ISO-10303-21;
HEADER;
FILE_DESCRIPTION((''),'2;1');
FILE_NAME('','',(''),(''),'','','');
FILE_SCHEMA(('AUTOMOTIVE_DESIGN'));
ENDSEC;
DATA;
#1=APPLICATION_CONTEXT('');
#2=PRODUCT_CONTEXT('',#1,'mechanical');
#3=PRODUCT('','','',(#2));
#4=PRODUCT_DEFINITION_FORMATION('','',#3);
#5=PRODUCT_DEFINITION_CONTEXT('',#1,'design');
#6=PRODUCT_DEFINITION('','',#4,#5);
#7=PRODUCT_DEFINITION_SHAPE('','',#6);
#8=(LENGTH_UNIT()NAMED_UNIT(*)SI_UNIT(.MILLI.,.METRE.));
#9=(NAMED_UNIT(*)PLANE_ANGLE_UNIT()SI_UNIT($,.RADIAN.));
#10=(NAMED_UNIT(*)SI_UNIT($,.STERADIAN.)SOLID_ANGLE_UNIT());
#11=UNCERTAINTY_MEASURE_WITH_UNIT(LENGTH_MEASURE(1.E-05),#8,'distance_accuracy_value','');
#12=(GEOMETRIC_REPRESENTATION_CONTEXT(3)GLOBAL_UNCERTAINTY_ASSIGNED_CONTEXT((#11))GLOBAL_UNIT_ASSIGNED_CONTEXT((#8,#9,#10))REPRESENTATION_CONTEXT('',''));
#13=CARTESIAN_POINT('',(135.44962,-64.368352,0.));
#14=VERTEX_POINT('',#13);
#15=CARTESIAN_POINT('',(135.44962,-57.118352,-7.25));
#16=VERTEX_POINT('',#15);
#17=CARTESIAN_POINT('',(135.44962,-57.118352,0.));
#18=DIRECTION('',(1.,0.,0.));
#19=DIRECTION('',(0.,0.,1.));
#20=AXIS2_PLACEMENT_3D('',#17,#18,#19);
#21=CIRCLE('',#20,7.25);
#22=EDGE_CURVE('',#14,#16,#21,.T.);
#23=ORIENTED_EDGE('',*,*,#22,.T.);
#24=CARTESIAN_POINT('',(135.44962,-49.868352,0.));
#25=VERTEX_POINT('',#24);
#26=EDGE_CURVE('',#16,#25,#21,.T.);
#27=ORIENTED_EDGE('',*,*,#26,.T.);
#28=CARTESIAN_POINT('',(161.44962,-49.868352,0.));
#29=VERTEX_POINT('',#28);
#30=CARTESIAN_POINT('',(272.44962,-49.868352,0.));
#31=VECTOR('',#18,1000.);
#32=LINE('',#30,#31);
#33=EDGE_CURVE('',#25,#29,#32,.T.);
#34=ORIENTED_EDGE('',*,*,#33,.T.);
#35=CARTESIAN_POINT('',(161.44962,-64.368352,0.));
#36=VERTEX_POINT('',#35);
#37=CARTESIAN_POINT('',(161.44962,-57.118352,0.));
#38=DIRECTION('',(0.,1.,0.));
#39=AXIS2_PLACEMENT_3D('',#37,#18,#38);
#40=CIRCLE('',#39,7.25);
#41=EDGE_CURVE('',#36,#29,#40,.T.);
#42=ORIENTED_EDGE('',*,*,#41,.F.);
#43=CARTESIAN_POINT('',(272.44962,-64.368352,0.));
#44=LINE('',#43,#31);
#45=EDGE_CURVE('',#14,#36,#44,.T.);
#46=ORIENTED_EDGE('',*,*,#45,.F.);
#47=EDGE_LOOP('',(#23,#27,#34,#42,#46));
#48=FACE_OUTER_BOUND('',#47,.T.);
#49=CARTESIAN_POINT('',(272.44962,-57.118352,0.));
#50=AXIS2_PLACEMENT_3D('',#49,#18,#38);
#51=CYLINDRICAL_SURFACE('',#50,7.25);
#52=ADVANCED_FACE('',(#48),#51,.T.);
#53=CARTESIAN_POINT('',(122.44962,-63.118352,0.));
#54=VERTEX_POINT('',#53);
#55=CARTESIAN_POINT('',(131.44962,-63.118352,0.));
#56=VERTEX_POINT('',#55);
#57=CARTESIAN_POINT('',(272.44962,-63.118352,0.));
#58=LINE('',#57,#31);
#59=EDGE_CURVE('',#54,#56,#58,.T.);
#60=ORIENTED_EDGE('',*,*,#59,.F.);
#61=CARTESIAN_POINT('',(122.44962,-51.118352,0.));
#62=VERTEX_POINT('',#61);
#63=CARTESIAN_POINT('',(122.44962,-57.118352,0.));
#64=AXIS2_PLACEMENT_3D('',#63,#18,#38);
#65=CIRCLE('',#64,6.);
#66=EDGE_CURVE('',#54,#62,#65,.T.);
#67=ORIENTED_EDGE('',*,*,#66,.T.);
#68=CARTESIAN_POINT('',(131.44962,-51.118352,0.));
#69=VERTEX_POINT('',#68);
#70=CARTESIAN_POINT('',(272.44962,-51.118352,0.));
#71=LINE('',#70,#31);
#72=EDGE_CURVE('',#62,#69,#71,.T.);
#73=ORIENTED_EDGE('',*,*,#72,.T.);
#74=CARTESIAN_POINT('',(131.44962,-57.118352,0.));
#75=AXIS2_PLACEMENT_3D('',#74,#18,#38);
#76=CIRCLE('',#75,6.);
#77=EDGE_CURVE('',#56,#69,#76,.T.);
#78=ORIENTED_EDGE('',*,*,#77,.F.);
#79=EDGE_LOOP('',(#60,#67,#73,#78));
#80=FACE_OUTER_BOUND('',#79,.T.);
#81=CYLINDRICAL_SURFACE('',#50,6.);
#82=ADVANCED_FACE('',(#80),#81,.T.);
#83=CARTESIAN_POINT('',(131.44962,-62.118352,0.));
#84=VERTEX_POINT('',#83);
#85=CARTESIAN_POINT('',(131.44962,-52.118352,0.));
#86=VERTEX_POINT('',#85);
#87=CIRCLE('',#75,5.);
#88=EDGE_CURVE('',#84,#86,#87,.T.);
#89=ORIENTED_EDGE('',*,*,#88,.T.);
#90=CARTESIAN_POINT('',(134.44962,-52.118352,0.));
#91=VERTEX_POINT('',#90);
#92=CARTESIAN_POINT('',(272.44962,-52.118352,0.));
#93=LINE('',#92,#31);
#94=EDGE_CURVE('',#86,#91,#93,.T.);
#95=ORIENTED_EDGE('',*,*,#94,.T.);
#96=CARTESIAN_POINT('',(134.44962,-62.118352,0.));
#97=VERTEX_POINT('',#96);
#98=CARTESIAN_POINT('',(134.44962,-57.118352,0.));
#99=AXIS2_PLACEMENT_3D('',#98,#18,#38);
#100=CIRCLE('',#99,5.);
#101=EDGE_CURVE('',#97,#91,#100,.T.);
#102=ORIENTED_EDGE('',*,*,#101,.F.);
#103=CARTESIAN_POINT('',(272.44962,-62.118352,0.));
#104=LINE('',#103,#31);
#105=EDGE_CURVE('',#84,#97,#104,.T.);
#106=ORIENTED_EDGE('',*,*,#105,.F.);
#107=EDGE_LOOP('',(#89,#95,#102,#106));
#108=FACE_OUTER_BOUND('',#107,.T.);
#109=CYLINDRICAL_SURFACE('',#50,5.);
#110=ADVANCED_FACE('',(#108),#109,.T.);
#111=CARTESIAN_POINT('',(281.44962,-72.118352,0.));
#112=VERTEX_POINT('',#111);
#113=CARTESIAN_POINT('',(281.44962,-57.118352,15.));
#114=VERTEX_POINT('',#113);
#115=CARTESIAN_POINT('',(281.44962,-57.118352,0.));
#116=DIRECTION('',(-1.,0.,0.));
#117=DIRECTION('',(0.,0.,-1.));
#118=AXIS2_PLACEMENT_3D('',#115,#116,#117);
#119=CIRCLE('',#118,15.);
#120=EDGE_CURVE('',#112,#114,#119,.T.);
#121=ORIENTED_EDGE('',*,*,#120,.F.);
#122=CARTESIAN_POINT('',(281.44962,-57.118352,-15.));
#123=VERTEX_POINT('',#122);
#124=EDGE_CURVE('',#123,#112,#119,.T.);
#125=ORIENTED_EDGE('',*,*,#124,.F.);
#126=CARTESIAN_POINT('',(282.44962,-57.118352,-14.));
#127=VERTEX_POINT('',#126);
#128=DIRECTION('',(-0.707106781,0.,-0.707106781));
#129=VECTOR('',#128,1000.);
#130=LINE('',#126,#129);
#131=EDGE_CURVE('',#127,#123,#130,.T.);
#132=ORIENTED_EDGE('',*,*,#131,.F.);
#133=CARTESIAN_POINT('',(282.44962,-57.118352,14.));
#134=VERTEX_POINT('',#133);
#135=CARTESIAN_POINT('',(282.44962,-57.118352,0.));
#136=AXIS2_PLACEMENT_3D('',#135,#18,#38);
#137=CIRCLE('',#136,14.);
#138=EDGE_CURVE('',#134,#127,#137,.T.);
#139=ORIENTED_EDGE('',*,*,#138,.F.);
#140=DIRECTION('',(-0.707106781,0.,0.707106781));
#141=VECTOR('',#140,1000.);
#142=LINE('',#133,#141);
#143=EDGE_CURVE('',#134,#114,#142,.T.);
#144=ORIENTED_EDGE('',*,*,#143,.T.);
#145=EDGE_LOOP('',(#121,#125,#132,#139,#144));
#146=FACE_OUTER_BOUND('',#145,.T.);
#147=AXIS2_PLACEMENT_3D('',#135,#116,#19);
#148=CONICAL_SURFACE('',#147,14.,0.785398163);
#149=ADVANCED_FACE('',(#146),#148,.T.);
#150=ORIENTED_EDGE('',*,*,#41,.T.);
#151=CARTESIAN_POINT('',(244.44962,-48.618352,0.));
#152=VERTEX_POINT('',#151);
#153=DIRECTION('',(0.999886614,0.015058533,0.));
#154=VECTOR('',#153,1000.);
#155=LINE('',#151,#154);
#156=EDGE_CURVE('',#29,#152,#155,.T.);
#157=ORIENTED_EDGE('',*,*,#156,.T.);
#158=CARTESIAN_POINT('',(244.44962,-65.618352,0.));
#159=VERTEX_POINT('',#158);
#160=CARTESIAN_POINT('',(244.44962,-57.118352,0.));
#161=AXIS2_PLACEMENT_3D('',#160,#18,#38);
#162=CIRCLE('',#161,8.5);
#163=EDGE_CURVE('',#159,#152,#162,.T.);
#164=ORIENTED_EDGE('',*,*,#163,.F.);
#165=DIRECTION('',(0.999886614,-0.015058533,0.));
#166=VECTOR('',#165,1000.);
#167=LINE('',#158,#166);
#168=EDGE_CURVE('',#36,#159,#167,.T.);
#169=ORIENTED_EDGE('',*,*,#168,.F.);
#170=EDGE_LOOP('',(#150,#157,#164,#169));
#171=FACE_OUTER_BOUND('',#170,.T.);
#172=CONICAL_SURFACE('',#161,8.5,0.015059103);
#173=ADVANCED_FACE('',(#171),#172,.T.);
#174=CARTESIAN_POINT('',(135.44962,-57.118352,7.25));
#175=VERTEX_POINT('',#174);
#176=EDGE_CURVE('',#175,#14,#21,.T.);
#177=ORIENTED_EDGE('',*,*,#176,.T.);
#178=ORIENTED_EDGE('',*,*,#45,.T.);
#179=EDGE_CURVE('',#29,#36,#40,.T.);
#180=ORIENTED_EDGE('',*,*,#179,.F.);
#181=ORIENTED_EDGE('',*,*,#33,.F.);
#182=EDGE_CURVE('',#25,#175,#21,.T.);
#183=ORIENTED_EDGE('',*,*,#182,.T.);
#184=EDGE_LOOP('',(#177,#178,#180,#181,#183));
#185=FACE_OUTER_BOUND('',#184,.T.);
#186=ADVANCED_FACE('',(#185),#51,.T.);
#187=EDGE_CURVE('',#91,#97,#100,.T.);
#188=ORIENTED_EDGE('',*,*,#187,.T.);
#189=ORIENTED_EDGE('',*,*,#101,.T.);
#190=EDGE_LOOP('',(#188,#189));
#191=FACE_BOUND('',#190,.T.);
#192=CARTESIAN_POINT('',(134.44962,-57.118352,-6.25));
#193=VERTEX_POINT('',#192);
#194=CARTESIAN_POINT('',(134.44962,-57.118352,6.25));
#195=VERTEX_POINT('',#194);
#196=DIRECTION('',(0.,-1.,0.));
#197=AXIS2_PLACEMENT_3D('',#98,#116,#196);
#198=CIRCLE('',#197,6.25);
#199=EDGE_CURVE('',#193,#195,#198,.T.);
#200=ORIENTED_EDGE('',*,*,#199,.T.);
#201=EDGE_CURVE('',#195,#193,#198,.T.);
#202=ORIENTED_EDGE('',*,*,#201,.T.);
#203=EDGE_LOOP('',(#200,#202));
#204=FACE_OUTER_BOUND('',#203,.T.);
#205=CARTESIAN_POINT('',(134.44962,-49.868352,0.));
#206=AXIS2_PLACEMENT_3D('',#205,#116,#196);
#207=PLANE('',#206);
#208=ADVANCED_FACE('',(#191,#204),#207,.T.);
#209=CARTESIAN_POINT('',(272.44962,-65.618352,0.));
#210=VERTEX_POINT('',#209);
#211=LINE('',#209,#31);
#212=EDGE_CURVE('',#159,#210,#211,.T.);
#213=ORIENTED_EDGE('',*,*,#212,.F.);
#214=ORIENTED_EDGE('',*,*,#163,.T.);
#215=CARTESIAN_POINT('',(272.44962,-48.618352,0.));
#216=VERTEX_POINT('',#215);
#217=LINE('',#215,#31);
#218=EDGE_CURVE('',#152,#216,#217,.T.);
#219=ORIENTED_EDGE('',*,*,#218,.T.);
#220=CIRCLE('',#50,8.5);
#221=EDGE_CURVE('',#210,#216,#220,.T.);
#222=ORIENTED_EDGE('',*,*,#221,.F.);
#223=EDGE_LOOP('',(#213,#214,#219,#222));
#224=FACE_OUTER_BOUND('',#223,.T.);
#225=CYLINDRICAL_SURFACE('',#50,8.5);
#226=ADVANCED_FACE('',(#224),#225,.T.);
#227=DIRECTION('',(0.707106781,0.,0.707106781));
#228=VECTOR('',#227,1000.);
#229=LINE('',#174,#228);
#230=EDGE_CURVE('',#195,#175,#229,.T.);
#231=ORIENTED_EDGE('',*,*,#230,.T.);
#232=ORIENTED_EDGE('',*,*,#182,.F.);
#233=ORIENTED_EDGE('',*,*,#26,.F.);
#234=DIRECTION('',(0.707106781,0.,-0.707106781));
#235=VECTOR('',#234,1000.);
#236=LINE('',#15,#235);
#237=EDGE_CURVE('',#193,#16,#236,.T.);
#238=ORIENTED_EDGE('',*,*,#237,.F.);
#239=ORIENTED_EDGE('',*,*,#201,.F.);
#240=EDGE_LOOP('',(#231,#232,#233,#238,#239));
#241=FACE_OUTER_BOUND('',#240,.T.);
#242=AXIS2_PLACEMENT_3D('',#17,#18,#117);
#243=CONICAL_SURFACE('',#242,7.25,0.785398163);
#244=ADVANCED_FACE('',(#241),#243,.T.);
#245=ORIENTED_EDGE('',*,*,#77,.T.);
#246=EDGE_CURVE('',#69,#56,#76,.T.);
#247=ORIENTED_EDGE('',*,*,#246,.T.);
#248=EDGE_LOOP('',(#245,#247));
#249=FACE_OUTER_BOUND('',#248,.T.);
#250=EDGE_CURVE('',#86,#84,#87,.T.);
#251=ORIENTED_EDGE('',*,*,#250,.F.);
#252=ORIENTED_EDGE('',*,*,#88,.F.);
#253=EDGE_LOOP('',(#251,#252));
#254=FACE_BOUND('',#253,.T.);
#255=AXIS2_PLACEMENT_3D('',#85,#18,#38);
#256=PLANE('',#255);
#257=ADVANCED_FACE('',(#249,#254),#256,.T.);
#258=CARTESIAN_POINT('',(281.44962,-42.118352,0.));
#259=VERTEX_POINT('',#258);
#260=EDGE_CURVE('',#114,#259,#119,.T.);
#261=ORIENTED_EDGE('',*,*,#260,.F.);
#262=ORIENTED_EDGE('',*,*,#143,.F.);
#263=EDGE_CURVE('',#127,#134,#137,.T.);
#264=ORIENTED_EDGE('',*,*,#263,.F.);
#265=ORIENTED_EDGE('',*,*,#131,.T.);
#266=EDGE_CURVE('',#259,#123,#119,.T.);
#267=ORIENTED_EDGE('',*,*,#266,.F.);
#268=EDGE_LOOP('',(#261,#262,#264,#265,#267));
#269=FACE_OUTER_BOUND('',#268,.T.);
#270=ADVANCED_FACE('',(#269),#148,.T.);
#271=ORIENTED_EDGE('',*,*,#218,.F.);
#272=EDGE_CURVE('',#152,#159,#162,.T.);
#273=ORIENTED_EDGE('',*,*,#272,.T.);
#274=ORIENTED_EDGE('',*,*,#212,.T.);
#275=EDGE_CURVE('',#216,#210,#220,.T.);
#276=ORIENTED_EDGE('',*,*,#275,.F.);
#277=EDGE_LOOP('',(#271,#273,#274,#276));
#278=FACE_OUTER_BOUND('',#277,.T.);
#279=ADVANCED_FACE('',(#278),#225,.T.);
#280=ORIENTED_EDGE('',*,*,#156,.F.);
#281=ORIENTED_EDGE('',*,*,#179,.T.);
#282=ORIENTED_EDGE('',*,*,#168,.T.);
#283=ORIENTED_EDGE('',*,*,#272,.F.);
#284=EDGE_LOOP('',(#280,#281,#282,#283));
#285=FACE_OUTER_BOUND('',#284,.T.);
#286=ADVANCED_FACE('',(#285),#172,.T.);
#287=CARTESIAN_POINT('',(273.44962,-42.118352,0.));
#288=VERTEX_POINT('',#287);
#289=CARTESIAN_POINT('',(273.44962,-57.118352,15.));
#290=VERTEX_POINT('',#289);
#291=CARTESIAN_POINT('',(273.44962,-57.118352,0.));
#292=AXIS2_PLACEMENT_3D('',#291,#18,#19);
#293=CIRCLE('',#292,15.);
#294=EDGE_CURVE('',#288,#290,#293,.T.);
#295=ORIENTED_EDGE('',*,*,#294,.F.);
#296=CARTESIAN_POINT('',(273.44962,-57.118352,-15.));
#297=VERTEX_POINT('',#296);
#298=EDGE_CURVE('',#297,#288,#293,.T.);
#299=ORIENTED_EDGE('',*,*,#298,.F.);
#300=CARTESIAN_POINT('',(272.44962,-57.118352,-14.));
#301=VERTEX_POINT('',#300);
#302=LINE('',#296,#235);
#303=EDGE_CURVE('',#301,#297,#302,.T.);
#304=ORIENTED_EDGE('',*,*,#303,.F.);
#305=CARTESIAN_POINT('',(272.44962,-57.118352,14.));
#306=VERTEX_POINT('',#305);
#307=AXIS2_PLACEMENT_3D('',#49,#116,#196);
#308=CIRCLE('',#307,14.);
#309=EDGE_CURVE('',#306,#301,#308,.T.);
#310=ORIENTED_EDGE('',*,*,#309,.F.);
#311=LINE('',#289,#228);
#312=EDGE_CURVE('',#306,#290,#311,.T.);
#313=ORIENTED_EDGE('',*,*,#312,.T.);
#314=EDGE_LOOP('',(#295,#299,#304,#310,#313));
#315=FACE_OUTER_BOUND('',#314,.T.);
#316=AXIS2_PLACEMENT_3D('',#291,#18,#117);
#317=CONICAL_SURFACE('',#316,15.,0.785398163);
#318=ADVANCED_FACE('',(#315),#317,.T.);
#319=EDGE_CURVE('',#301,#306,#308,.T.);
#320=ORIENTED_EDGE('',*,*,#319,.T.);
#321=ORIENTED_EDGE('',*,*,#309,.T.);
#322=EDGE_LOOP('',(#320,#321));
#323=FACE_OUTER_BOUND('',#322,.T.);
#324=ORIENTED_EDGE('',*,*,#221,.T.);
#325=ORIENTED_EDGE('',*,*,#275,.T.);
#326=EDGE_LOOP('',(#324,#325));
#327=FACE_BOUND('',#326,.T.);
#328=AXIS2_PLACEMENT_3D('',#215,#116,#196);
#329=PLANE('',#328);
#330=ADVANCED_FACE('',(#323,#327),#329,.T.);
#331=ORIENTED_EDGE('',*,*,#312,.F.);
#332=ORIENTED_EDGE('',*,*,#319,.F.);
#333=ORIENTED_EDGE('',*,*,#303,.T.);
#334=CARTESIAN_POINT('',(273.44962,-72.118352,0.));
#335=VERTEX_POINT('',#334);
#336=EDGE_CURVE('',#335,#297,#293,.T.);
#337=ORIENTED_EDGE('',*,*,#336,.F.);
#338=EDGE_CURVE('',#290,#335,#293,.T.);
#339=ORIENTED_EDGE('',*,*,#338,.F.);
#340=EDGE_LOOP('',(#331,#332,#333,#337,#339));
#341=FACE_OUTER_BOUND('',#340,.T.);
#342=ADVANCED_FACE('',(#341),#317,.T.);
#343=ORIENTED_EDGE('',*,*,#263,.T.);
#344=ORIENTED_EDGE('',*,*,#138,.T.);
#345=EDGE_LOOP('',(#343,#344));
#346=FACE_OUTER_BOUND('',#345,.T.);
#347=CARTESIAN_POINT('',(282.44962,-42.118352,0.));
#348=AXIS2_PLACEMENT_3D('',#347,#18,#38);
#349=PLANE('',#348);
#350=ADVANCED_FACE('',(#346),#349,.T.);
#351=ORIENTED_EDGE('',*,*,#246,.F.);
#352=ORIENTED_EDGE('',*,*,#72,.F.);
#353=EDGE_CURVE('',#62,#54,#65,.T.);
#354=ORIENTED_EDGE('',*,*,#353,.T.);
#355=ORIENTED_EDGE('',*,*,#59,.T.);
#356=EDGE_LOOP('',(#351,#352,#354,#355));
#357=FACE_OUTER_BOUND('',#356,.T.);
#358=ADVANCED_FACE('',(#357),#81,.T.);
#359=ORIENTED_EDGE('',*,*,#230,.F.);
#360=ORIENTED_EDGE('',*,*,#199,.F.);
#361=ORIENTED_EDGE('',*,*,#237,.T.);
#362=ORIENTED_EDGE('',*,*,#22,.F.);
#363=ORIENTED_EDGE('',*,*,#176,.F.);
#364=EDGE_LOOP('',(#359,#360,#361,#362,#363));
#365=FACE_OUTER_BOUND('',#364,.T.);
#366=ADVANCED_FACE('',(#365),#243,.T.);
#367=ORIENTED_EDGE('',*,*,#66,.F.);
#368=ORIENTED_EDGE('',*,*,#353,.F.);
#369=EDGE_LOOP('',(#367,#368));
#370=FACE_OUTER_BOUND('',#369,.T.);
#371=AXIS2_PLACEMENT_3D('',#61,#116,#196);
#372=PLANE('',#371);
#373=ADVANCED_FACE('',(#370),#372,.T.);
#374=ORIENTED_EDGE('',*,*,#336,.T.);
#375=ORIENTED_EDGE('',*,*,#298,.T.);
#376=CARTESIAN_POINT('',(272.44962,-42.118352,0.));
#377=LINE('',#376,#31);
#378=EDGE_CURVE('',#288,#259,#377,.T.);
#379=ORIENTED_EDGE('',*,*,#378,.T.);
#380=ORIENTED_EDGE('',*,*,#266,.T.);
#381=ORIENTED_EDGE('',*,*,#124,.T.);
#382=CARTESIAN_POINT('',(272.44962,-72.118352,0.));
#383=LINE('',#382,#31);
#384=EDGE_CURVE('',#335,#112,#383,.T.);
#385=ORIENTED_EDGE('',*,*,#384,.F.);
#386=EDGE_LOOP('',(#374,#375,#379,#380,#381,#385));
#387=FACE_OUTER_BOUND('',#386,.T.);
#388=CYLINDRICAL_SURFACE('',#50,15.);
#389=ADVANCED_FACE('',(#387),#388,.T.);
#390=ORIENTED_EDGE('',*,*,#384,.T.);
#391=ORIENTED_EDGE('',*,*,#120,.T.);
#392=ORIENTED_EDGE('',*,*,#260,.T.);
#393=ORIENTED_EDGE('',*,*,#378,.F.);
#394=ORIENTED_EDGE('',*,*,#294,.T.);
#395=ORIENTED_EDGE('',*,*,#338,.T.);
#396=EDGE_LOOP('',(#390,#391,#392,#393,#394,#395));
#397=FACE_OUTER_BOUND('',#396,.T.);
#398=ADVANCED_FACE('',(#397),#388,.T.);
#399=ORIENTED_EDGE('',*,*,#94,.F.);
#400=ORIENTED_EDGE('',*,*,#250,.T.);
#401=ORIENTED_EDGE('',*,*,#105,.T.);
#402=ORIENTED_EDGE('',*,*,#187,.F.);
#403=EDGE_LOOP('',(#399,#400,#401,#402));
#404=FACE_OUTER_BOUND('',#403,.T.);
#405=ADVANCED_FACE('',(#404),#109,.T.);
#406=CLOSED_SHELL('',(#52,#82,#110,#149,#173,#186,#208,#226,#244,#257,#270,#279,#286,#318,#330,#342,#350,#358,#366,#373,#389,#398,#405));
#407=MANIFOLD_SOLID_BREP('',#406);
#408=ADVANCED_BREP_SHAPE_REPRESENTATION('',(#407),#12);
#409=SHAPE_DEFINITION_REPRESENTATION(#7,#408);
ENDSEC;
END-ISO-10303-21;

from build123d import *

# Parameters (mm, degrees)
CHAMFER_1_SIZE = 1


with BuildPart() as part:
    # 草图1 → 旋转1 (revolve)
    with BuildSketch(Plane.XY):
        Polygon((134.449619949, -49.868352239), (161.449619949, -49.868352239), (244.449619949, -48.618352239), (272.449619949, -48.618352239), (272.449619949, -42.118352239), (282.449619949, -42.118352239), (282.449619949, -57.118352239), (122.449619949, -57.118352239), (122.449619949, -51.118352239), (131.449619949, -51.118352239), (131.449619949, -52.118352239), (134.449619949, -52.118352239), align=None)
    revolve(axis=Axis((272.449619949, -57.118352239, 0), (-1, 0, 0)))

    # 倒角1
    chamfer_1_edges = [part.edges().sort_by_distance(p)[0] for p in [
        (282.449619949, -72.118352239, 0),
        (272.449619949, -72.118352239, 0),
        (134.449619949, -64.368352239, 0),
    ]]
    chamfer(chamfer_1_edges, length=CHAMFER_1_SIZE)


solid = part.part
